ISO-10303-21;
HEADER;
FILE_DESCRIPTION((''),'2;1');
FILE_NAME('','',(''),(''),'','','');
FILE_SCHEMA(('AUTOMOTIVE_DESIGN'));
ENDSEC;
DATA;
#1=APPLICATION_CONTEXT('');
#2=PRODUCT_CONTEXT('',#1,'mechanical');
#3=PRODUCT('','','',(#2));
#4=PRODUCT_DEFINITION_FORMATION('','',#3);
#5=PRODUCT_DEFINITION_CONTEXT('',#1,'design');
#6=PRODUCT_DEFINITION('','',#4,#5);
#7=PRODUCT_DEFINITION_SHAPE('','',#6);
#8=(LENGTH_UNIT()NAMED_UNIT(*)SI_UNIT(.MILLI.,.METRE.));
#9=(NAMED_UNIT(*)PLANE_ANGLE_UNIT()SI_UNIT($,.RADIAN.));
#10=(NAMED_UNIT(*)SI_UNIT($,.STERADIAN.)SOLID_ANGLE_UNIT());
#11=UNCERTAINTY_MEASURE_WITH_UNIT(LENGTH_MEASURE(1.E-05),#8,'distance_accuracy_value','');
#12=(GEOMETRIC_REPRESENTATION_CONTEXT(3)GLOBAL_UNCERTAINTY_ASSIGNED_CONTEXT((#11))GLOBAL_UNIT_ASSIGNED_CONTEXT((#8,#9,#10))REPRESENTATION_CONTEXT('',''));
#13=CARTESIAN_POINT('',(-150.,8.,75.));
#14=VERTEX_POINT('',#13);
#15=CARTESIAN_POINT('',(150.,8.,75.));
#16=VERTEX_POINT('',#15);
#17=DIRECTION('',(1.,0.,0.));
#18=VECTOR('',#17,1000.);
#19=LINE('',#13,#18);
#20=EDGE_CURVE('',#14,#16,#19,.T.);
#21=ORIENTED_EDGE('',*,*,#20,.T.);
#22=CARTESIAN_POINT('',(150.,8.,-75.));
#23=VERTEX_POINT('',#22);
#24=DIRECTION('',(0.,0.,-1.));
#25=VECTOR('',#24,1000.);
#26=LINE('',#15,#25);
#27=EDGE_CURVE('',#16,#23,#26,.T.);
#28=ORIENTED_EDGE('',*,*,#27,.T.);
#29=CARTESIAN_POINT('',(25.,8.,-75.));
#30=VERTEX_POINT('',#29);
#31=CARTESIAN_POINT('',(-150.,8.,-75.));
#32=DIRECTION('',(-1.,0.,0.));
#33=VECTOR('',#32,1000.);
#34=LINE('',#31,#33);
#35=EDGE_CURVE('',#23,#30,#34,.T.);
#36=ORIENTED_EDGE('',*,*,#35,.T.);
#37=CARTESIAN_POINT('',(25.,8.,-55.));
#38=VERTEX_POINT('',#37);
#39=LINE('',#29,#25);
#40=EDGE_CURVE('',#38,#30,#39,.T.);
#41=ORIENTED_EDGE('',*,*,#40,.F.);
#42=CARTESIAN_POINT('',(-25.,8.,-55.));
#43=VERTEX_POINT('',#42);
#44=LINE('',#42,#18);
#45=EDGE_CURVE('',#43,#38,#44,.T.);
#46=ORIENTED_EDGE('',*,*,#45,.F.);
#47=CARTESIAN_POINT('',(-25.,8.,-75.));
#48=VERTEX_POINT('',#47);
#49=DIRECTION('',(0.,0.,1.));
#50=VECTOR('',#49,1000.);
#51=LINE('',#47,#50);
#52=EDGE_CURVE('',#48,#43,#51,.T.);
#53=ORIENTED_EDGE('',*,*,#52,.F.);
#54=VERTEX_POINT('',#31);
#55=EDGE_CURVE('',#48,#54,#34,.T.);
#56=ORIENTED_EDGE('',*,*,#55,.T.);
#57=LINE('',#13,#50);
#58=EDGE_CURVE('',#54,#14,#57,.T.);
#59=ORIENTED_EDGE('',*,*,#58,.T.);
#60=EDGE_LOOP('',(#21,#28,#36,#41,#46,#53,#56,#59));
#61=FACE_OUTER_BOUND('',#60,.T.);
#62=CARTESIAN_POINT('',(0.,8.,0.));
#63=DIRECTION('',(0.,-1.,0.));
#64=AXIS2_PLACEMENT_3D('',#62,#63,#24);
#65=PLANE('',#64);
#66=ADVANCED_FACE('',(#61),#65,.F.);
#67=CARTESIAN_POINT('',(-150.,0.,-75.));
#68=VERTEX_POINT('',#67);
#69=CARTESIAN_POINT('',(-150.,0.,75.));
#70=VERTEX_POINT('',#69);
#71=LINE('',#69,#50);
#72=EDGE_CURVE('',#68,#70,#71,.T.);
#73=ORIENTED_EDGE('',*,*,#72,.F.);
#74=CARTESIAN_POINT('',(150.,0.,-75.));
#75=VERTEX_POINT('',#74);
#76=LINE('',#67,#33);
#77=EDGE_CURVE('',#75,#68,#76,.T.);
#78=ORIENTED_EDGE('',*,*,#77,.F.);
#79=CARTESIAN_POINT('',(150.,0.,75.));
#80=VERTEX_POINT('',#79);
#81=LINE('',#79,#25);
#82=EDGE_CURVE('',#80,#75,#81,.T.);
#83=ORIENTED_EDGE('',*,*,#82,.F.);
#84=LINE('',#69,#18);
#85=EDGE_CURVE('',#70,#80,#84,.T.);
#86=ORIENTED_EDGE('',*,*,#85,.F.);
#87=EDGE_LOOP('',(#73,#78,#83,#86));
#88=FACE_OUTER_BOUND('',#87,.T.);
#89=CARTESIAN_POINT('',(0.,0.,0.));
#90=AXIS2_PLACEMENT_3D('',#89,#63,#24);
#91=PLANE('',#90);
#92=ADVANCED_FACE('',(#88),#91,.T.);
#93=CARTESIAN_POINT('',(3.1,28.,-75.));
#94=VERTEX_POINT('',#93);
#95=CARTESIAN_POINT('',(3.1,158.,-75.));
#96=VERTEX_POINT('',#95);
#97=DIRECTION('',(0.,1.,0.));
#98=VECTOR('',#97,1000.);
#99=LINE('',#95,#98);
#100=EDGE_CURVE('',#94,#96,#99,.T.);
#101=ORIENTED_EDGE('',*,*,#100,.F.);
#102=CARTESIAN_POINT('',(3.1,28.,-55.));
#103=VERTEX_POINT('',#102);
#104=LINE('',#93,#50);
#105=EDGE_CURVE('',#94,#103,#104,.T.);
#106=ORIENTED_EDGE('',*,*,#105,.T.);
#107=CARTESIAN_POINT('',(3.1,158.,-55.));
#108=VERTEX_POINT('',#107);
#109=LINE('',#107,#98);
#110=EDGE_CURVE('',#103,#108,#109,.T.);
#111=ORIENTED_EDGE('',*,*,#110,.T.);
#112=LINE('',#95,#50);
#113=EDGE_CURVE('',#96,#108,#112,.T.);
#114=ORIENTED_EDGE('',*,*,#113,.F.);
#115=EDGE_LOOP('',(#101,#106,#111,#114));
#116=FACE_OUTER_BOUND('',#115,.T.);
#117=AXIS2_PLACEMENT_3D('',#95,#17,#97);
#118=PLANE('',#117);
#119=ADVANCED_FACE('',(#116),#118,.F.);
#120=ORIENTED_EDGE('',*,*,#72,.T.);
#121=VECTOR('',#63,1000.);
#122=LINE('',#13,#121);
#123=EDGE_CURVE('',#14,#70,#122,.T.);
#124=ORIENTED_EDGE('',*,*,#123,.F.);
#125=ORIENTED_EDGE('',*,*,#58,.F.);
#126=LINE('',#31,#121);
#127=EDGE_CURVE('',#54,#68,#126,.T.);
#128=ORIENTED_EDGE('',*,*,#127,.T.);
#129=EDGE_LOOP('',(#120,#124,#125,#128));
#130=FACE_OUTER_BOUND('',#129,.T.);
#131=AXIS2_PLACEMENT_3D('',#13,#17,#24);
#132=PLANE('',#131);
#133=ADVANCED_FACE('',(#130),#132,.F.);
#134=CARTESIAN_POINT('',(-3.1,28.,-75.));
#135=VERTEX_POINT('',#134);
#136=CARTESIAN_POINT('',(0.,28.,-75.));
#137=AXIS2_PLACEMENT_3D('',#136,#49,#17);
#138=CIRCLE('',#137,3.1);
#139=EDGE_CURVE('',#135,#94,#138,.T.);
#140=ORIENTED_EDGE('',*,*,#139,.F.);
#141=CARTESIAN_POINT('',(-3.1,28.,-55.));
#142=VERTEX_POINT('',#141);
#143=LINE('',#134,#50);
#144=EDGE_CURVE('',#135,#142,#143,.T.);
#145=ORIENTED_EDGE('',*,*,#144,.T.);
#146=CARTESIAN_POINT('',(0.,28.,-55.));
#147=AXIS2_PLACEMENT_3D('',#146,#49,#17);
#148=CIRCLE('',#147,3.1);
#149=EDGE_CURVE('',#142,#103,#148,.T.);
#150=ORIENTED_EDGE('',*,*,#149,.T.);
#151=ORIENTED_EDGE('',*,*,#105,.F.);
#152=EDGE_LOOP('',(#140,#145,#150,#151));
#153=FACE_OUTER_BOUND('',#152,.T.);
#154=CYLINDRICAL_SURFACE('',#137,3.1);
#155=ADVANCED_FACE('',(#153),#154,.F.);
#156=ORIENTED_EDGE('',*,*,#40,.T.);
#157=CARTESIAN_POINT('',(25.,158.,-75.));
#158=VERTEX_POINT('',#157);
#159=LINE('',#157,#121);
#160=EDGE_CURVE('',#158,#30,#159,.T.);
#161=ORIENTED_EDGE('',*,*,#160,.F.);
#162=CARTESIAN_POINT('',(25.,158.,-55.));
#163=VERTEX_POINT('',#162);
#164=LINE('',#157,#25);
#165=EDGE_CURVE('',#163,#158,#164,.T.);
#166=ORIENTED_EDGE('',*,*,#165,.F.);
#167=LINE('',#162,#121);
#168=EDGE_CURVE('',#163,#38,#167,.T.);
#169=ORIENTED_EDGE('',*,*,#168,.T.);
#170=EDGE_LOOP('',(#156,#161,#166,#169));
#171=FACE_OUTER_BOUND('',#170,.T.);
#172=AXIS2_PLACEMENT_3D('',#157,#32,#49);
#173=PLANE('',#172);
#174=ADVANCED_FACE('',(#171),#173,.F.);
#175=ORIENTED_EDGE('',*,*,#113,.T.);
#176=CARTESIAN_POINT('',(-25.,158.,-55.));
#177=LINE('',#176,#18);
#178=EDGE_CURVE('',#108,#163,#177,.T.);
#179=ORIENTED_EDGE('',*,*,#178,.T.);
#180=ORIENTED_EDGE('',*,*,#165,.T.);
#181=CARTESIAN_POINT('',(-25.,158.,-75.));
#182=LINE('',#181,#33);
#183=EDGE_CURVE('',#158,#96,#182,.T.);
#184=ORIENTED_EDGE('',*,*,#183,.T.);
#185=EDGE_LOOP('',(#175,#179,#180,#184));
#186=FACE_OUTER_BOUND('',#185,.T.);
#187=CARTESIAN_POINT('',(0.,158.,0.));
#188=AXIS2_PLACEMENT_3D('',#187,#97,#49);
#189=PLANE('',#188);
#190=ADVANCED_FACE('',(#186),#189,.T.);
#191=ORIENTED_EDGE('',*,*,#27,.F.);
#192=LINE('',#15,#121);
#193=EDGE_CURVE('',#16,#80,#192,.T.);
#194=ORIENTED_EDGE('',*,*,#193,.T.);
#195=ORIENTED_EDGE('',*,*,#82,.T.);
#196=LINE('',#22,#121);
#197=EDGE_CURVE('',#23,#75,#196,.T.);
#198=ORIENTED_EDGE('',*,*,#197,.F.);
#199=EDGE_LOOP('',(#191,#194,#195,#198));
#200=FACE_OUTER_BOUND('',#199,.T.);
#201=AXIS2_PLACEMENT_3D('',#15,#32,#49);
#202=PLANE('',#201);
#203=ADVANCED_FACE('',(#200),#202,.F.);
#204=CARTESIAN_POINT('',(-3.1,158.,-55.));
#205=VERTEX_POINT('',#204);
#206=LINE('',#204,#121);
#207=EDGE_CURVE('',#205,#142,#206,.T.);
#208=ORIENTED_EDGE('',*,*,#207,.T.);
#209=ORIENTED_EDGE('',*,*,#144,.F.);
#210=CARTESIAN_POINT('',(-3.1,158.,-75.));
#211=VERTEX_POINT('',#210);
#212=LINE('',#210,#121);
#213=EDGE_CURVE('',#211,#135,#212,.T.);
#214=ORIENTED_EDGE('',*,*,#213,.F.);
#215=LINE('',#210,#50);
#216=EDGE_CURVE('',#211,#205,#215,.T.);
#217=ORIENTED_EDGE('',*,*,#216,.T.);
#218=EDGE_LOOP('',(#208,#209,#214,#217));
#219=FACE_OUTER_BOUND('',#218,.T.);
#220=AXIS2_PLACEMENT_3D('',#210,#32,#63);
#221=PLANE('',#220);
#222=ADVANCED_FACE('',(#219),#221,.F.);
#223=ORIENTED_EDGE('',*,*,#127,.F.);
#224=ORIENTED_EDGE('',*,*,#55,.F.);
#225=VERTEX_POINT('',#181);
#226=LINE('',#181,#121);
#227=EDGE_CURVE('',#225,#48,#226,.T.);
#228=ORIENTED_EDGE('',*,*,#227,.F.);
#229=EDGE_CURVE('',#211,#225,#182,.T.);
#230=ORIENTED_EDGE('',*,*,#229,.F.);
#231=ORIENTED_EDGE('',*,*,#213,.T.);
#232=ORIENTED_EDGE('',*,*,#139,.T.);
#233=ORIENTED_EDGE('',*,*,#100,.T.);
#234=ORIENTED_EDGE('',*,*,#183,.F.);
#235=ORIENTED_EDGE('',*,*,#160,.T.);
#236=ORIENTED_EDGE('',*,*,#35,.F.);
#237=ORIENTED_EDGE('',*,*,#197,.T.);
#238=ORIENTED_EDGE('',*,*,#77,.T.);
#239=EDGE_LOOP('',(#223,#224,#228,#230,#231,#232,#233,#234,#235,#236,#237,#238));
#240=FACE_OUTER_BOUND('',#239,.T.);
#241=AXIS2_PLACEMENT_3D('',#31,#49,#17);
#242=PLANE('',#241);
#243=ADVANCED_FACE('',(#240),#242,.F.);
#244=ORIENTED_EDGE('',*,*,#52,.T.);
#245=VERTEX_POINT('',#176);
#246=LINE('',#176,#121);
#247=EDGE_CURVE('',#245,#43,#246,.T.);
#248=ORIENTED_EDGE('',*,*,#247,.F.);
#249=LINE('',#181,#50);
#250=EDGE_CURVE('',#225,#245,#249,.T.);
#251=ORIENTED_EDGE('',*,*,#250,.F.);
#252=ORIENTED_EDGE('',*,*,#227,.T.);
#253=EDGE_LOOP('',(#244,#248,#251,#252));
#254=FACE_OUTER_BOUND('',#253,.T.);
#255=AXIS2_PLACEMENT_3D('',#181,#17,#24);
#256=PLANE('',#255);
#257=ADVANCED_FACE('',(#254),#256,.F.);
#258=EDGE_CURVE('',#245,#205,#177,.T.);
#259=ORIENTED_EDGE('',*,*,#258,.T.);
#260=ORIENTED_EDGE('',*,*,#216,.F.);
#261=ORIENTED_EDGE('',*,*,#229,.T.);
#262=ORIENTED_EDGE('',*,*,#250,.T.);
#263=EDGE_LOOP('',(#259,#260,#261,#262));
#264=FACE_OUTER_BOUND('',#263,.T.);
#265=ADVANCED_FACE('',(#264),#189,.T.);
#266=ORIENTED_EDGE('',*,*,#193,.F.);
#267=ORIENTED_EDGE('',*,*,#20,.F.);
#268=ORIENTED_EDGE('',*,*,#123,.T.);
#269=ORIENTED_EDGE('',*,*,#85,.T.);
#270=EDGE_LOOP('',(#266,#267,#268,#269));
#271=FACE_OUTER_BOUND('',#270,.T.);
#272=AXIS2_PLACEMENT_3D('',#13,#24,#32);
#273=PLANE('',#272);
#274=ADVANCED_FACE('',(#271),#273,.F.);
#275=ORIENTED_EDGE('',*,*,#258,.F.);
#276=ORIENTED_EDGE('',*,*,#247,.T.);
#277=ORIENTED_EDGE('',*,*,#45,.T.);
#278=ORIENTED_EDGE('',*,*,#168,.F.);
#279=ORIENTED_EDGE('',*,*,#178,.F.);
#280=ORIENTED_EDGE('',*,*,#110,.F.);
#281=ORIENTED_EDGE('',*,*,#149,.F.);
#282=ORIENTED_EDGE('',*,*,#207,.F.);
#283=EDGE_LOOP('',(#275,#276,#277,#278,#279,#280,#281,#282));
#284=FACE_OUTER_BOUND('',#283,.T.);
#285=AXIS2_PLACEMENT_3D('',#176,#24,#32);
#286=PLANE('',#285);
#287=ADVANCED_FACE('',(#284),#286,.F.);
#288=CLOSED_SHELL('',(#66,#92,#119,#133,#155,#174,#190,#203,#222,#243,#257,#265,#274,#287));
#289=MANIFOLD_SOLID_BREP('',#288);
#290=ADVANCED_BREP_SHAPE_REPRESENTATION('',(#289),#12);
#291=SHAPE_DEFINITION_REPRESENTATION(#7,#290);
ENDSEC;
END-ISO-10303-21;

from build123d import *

# Parameters (mm, degrees)
SKETCH1_W           = 300
SKETCH1_H           = 150
BOSS_EXTRUDE1_DEPTH = 8
SKETCH2_W           = 50
SKETCH2_H           = 20
BOSS_EXTRUDE2_DEPTH = 150
CUT_EXTRUDE1_DEPTH  = 254.700610957


with BuildPart() as part:
    # Sketch1 → Boss-Extrude1 (new body)
    with BuildSketch(Plane(origin=(0, 0, 0), x_dir=(1, 0, 0), z_dir=(0, 1, 0))):
        Rectangle(SKETCH1_W, SKETCH1_H)
    extrude(amount=BOSS_EXTRUDE1_DEPTH)

    # Sketch2 → Boss-Extrude2 (add)
    with BuildSketch(Plane(origin=(0, 8, 0), x_dir=(1, 0, 0), z_dir=(0, 1, 0))):
        with Locations((0, 65)):
            Rectangle(SKETCH2_W, SKETCH2_H)
    extrude(amount=BOSS_EXTRUDE2_DEPTH)

    # Sketch3 → Cut-Extrude1 (cut, through all)
    with BuildSketch(Plane.XY.offset(-55)):
        with BuildLine():
            Line((3.1, 158), (3.1, 28))
            ThreePointArc((3.1, 28), (0, 24.9), (-3.1, 28))
            Line((-3.1, 28), (-3.1, 158))
            ThreePointArc((-3.1, 158), (0, 161.1), (3.1, 158))
        make_face()
    extrude(amount=-CUT_EXTRUDE1_DEPTH, mode=Mode.SUBTRACT)


solid = part.part
